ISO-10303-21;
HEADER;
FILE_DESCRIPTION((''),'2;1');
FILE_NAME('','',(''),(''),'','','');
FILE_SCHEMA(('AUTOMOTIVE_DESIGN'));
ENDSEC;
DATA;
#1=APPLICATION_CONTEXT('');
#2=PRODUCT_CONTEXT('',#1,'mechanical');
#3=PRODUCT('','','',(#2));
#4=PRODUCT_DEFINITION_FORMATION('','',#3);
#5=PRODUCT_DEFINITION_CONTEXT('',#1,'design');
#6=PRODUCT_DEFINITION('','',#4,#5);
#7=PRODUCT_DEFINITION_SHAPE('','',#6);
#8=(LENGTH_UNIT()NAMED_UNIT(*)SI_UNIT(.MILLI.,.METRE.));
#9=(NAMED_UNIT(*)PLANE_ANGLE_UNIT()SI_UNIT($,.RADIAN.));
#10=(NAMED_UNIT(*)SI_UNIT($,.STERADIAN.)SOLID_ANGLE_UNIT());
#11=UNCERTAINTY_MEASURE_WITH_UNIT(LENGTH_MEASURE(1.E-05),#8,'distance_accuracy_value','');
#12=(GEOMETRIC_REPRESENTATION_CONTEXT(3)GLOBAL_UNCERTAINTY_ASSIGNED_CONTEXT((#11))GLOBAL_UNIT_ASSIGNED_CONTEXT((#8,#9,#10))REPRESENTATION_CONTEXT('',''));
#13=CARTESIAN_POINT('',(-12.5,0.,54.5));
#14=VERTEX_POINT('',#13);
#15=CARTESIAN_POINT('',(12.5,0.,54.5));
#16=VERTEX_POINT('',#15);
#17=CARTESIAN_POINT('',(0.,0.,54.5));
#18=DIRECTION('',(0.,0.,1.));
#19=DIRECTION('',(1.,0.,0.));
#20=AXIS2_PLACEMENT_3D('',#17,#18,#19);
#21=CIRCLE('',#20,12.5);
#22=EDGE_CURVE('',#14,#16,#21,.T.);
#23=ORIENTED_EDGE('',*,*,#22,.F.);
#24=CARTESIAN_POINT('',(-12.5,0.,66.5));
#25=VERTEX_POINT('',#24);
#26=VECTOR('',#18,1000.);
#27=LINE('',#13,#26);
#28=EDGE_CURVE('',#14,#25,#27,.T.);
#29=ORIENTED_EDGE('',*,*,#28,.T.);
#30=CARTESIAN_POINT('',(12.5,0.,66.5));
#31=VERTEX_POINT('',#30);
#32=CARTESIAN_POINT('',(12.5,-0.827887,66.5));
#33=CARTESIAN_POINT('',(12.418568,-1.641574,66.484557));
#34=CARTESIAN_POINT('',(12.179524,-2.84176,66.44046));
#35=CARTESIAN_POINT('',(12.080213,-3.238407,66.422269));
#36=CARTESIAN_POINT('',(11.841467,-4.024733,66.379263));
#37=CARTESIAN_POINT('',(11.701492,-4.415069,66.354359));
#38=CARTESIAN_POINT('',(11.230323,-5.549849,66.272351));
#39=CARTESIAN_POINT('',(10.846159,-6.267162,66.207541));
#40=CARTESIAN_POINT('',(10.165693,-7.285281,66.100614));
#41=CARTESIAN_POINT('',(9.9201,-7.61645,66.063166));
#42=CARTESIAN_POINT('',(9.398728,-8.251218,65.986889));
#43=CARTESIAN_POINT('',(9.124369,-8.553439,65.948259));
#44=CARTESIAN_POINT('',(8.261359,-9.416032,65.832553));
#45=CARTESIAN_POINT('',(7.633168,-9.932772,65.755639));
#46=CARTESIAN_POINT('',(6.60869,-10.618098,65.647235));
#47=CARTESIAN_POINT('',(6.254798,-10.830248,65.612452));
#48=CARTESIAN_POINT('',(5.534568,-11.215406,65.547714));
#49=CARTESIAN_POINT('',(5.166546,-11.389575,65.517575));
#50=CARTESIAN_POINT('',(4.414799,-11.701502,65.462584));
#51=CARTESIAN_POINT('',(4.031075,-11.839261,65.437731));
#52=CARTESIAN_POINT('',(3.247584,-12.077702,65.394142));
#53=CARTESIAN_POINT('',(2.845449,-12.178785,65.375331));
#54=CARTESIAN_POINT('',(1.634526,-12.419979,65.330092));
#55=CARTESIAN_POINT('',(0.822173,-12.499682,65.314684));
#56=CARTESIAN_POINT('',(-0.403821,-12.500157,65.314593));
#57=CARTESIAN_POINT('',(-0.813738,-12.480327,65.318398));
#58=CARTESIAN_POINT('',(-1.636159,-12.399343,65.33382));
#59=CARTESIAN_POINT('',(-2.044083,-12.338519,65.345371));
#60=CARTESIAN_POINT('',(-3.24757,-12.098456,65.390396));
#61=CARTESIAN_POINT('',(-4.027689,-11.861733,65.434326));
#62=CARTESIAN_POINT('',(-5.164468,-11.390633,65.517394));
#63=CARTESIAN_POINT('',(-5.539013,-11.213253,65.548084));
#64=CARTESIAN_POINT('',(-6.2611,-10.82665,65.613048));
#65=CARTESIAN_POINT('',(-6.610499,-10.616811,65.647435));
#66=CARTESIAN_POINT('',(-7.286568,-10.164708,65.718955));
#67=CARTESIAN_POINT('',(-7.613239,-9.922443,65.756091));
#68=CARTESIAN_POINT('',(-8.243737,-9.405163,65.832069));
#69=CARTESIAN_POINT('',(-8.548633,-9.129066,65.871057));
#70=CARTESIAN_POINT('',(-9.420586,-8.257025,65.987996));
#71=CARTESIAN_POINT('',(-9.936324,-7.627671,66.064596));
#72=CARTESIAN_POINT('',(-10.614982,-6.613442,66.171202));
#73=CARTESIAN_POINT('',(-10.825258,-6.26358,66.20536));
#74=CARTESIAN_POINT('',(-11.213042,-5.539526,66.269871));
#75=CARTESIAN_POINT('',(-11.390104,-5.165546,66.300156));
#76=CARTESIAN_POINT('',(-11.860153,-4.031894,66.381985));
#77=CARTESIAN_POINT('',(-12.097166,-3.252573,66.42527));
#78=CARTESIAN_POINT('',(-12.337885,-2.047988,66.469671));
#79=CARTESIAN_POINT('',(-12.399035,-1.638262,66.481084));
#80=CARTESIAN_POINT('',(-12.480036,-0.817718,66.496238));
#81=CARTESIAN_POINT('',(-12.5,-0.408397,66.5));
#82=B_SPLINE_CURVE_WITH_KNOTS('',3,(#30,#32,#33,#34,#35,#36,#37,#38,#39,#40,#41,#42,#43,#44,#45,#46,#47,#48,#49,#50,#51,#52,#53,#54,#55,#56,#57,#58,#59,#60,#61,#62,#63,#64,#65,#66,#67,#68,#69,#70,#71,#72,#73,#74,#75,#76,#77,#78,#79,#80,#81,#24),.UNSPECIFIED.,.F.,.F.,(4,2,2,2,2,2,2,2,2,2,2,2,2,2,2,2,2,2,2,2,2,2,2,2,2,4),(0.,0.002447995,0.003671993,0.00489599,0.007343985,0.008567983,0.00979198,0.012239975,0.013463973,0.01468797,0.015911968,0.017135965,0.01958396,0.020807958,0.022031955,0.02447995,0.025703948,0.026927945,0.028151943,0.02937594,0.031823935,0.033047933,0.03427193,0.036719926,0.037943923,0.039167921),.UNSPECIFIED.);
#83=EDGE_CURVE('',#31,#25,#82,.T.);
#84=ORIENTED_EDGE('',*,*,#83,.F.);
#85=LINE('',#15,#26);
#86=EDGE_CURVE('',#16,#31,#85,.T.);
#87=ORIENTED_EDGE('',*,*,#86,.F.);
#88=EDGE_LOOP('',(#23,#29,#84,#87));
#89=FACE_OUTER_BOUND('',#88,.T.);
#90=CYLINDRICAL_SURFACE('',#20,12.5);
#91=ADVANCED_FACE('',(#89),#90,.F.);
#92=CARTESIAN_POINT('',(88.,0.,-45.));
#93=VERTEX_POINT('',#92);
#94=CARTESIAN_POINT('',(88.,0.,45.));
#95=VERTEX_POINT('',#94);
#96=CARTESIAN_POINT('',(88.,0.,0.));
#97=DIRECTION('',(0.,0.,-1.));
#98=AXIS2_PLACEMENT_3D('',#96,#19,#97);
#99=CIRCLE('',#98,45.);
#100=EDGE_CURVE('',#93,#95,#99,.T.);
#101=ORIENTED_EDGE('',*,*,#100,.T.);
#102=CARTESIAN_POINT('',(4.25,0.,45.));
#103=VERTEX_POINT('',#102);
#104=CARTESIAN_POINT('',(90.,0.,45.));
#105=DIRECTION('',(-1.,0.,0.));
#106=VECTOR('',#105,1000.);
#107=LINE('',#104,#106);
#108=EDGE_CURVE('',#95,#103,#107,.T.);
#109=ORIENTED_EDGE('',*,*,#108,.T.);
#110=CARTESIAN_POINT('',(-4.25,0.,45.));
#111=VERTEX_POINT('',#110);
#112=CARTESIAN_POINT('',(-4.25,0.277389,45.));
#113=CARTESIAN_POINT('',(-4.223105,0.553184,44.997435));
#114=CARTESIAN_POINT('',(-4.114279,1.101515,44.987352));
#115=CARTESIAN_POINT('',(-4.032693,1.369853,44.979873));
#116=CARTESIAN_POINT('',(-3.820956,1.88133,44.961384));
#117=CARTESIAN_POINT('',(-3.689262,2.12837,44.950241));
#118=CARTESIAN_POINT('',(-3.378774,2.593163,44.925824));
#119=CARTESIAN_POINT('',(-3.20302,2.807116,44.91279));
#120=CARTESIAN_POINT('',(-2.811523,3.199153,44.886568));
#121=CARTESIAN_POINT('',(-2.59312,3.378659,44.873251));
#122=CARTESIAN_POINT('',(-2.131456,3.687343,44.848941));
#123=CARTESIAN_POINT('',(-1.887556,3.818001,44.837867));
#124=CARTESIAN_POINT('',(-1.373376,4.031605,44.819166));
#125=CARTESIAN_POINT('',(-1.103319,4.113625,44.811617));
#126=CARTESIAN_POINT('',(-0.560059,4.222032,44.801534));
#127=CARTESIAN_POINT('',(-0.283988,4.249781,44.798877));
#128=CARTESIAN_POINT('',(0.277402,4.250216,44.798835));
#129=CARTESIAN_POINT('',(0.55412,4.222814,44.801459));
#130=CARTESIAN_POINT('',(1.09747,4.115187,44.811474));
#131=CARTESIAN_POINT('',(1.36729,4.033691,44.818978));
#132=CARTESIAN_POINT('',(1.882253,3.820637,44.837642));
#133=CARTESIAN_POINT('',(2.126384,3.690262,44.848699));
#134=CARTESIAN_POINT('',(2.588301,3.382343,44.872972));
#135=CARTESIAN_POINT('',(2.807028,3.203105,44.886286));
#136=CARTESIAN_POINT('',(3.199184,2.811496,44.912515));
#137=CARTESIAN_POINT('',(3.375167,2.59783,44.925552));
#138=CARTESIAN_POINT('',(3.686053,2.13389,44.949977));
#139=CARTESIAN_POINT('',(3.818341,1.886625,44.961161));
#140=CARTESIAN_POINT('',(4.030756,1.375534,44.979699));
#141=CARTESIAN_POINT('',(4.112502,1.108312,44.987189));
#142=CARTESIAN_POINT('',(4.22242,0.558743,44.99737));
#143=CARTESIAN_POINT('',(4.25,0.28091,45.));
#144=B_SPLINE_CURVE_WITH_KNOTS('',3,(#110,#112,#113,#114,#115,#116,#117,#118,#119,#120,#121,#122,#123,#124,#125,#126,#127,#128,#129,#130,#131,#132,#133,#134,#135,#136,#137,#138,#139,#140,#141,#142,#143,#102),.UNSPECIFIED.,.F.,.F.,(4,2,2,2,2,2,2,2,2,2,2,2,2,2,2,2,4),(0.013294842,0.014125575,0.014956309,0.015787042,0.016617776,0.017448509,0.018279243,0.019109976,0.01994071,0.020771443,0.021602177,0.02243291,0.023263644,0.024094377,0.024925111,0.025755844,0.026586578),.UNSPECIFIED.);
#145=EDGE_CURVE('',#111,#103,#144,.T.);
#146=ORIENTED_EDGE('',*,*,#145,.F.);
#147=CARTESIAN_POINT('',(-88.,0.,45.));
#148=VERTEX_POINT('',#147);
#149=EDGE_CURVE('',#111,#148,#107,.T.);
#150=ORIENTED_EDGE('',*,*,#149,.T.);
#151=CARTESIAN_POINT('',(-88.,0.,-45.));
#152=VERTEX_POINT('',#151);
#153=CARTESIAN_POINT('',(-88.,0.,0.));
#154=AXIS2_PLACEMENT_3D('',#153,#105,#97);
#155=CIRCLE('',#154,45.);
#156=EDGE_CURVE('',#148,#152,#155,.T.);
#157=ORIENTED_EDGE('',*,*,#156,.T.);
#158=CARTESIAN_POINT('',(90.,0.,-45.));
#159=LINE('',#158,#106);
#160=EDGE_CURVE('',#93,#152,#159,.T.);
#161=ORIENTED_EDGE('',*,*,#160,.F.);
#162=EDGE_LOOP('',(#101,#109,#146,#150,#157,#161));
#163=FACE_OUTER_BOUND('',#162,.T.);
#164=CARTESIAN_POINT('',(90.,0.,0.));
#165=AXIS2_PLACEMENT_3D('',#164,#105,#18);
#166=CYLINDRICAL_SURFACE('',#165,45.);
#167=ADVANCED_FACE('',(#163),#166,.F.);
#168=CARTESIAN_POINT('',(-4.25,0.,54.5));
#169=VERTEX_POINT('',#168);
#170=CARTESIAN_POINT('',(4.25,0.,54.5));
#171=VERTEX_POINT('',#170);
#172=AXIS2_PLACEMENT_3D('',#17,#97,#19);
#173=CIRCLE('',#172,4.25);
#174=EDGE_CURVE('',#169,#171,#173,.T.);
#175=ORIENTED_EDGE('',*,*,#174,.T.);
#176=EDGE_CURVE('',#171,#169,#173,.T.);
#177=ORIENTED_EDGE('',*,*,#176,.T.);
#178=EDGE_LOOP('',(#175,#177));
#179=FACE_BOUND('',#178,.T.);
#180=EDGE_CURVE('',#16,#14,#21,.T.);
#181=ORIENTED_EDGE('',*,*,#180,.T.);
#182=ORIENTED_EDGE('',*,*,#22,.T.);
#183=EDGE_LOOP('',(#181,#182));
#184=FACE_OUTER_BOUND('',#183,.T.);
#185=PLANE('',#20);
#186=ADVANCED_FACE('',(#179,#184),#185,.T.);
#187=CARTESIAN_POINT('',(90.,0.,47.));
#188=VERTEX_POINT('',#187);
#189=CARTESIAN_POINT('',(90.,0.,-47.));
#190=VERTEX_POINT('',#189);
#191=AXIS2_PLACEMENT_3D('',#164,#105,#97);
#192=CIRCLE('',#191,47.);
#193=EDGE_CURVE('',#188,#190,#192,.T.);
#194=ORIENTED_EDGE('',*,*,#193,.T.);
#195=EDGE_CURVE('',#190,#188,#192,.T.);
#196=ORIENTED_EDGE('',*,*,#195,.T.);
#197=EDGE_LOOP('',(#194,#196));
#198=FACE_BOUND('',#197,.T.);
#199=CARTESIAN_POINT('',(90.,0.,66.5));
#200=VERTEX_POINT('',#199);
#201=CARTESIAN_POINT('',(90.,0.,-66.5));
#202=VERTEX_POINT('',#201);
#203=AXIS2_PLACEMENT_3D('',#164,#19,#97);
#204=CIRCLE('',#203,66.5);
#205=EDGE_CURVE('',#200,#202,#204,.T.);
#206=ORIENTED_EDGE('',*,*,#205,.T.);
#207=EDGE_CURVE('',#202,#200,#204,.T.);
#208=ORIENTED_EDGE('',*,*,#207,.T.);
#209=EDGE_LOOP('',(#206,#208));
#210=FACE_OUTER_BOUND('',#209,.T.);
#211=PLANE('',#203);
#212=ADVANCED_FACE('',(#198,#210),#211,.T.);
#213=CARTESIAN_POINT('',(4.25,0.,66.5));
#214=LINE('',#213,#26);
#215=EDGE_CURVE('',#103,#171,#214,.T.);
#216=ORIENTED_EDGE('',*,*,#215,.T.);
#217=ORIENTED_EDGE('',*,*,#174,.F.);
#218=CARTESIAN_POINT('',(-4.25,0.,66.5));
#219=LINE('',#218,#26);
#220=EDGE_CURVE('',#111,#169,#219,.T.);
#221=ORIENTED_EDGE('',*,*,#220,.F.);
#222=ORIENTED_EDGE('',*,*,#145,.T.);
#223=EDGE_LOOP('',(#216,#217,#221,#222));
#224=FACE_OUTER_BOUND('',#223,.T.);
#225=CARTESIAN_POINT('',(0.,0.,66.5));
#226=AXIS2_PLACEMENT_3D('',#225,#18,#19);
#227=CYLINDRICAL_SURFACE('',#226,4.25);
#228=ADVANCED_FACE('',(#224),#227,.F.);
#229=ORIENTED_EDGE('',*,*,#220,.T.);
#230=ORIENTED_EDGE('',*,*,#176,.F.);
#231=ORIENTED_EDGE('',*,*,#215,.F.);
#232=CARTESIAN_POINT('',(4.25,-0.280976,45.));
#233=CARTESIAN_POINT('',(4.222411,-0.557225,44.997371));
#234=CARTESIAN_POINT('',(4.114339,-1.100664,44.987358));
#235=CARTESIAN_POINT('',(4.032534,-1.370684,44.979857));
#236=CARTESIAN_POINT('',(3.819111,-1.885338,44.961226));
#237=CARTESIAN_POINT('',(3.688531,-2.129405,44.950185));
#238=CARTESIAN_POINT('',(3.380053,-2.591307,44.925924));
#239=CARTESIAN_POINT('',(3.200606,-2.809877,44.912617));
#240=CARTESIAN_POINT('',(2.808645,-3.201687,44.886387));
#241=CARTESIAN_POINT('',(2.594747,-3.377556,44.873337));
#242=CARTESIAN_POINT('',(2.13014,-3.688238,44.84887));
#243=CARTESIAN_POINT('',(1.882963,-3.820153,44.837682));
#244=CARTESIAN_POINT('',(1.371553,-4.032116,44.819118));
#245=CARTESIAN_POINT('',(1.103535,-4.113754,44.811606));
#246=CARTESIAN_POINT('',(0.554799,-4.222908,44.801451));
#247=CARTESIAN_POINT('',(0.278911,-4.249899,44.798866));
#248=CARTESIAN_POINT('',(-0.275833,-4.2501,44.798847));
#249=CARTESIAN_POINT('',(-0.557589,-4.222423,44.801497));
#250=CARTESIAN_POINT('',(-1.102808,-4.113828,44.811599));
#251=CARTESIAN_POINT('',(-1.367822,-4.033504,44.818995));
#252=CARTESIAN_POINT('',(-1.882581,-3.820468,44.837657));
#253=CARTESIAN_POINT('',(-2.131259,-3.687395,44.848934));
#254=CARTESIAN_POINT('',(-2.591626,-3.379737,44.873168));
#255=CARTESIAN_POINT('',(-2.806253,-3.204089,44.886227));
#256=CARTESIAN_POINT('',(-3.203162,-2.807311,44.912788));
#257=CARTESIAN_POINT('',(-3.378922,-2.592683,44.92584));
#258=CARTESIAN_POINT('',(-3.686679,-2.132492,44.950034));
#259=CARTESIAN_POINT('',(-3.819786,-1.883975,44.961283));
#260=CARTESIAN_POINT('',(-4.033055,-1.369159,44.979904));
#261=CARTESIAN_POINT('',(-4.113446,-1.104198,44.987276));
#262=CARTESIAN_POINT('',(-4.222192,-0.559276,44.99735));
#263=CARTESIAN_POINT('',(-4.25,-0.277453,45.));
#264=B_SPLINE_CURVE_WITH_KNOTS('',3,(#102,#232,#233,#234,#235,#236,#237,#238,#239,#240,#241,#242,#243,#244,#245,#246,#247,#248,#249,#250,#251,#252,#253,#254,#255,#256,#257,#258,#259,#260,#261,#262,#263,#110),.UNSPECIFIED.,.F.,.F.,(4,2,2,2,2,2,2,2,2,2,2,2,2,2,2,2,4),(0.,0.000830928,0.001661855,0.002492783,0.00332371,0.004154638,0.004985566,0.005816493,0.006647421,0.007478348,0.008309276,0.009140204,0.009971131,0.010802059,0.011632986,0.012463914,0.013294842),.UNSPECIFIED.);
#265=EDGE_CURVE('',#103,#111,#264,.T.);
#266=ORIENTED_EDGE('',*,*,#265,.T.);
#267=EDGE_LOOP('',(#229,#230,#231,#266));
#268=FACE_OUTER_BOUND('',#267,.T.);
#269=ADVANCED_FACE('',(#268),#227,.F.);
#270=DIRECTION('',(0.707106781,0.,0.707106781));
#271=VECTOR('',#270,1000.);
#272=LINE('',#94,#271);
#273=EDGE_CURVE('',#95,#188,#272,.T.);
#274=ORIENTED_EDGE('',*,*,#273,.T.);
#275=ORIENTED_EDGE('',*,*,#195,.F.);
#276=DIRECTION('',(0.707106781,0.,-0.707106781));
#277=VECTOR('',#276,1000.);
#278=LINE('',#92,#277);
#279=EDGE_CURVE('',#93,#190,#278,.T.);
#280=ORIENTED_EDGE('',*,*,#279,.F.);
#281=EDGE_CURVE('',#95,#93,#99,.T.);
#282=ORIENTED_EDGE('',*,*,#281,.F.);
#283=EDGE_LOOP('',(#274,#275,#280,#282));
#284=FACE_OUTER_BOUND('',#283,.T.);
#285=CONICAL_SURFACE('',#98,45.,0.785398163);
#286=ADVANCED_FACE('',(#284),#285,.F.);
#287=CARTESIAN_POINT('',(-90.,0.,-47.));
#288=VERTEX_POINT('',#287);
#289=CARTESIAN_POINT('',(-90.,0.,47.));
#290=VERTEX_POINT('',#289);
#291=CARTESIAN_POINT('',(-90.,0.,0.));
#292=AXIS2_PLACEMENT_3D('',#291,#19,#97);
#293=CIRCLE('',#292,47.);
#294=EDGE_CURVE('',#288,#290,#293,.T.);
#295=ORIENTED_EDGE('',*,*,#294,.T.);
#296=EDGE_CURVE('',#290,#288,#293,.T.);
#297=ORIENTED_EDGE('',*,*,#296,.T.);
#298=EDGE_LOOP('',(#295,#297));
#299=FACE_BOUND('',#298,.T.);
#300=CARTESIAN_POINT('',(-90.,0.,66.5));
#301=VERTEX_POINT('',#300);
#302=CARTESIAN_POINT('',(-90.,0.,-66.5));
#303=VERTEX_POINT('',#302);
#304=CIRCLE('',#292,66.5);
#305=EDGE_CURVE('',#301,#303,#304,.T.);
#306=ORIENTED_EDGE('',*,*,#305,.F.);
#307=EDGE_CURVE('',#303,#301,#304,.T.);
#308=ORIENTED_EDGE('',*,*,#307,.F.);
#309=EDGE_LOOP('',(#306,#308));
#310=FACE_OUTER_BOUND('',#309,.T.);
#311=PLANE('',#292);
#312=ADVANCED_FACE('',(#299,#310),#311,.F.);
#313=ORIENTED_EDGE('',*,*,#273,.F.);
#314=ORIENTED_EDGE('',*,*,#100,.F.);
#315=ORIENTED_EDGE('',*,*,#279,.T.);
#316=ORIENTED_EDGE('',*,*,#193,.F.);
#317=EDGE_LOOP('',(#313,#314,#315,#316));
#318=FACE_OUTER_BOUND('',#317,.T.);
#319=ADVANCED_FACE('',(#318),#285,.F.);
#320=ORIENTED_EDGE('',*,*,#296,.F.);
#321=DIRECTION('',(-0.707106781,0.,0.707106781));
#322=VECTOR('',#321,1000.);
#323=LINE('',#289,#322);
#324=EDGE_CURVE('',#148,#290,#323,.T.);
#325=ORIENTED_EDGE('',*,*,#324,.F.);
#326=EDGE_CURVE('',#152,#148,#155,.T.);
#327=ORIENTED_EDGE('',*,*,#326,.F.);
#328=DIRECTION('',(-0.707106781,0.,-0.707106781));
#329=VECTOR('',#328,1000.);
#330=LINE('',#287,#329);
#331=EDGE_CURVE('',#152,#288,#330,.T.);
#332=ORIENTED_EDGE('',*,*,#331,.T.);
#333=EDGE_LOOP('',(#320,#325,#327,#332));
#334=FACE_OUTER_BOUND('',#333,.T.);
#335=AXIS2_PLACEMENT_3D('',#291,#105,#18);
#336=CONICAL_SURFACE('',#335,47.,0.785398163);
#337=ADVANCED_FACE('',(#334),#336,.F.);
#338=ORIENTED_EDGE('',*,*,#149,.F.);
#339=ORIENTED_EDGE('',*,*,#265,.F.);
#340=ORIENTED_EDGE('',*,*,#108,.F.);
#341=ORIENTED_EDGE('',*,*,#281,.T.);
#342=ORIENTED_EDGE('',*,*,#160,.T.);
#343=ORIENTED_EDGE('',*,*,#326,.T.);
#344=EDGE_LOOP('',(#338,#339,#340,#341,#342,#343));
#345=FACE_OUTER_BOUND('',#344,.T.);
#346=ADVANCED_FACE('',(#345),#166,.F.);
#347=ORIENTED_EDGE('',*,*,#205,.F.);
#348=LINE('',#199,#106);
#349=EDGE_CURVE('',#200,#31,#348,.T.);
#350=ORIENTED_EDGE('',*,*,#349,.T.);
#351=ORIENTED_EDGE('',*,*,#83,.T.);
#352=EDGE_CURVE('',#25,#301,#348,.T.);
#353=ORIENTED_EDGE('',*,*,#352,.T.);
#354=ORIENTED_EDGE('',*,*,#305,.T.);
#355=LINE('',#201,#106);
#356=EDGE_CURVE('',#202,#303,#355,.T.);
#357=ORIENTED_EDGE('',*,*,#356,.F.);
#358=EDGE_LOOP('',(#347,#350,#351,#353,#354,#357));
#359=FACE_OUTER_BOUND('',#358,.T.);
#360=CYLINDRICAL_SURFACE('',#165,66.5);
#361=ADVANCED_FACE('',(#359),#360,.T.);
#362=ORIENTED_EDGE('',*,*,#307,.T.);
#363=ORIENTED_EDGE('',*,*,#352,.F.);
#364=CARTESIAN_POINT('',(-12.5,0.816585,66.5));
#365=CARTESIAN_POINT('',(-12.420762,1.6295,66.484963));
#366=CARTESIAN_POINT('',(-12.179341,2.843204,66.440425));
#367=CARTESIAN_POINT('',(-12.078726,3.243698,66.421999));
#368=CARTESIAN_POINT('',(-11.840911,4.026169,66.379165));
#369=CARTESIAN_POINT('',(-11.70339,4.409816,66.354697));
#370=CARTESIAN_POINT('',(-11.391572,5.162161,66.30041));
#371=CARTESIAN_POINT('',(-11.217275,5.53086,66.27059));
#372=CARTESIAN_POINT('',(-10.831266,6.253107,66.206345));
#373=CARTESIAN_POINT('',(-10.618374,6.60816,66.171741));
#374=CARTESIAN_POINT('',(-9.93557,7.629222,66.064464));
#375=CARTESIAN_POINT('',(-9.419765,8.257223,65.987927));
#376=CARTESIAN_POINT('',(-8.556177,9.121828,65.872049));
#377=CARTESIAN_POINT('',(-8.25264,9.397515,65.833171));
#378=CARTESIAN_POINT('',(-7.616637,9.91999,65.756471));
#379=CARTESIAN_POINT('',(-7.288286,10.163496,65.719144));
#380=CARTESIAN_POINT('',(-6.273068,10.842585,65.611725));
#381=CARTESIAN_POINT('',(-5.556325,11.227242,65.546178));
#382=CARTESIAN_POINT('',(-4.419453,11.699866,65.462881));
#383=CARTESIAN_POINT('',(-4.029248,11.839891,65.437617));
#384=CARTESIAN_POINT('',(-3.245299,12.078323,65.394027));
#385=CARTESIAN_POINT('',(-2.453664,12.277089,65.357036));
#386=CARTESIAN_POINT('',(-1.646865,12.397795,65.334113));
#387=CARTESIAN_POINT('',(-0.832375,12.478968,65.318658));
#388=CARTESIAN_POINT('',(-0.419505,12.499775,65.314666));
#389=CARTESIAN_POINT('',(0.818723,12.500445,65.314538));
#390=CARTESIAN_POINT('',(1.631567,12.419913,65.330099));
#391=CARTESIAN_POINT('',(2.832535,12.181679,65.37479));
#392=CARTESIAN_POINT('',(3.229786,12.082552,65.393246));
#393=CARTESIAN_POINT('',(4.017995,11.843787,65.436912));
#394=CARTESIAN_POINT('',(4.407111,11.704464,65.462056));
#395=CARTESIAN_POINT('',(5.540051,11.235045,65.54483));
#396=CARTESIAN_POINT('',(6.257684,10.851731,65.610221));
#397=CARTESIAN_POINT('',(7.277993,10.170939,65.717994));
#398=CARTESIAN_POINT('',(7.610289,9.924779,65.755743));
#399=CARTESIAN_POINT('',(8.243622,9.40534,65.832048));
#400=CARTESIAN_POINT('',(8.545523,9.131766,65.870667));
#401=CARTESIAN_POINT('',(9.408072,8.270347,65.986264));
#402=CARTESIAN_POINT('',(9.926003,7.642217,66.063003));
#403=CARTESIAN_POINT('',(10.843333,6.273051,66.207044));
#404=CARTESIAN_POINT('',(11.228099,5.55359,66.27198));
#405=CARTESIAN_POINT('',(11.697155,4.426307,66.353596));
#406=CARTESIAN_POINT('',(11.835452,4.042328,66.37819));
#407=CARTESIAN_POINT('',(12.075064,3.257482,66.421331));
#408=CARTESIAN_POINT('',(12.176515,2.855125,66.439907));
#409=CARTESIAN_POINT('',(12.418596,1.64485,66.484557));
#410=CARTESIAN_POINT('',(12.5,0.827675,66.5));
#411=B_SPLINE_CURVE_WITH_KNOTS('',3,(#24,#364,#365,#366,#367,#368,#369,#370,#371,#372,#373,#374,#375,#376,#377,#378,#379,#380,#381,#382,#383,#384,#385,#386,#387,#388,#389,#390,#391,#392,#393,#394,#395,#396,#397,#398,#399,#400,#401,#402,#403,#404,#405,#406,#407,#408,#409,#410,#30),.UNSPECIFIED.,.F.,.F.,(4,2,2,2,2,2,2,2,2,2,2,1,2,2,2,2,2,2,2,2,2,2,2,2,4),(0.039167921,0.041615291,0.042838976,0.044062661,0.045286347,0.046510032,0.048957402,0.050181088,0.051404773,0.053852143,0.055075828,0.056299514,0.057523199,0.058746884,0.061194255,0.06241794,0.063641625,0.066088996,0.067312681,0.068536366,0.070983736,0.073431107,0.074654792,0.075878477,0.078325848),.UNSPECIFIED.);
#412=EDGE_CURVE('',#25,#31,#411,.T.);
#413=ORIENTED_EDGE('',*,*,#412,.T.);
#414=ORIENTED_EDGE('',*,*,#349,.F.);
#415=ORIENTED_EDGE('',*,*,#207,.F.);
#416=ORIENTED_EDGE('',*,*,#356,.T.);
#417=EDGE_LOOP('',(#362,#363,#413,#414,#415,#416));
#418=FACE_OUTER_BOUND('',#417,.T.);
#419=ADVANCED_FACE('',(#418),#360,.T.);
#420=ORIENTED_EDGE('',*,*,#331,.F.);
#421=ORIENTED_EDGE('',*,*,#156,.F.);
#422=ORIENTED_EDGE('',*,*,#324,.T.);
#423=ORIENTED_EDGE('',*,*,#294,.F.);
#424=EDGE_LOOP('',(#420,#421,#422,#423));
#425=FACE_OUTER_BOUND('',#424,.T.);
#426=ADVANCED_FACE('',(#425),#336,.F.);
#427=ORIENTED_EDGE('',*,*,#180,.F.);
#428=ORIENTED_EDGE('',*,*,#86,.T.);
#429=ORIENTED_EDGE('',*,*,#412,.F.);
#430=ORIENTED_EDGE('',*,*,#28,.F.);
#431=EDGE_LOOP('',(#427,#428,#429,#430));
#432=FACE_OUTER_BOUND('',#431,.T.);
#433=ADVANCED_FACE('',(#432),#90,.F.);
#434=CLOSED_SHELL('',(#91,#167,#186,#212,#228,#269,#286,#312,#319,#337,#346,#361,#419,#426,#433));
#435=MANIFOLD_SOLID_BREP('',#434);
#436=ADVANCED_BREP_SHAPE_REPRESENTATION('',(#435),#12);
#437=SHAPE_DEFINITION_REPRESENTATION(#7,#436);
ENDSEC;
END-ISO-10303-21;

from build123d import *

# Parameters (mm, degrees)
SKETCH1_R              = 66.5
SKETCH1_R_2            = 45
BOSS_EXTRUDE1_DEPTH    = 90
M10_TAPPED_HOLE1_D     = 8.5
M10_TAPPED_HOLE1_DEPTH = 66.499
M10_TAPPED_HOLE1_TIP   = 2.553657631
SKETCH4_R              = 12.5
CUT_EXTRUDE1_DEPTH     = 12
CHAMFER1_SIZE          = 2


with BuildPart() as part:
    # Sketch1 → Boss-Extrude1 (new, symmetric)
    with BuildSketch(Plane(origin=(0, 0, 0), x_dir=(0, 0, -1), z_dir=(1, 0, 0))):
        with Locations(Location((0, 0, 0), (0, 0, 180))):
            Circle(SKETCH1_R)
        with Locations(Location((0, 0, 0), (0, 0, 180))):
            Circle(SKETCH1_R_2, mode=Mode.SUBTRACT)
    extrude(amount=BOSS_EXTRUDE1_DEPTH, both=True)

    # M10 Tapped Hole1
    with Locations(Plane.XY.offset(66.5)):
        with Locations((0, 0)):
            Hole(M10_TAPPED_HOLE1_D / 2, depth=M10_TAPPED_HOLE1_DEPTH)
            with Locations((0, 0, -(M10_TAPPED_HOLE1_DEPTH + M10_TAPPED_HOLE1_TIP / 2))):  # 118° drill point
                Cone(0, M10_TAPPED_HOLE1_D / 2, M10_TAPPED_HOLE1_TIP, mode=Mode.SUBTRACT)

    # Sketch4 → Cut-Extrude1 (cut)
    with BuildSketch(Plane.XY.offset(66.5)):
        Circle(SKETCH4_R)
    extrude(amount=-CUT_EXTRUDE1_DEPTH, mode=Mode.SUBTRACT)

    # Chamfer1
    chamfer1_edges = [part.edges().sort_by_distance(p)[0] for p in [
        (-90, 0, -45),
        (90, 0, -45),
    ]]
    chamfer(chamfer1_edges, length=CHAMFER1_SIZE)


solid = part.part
